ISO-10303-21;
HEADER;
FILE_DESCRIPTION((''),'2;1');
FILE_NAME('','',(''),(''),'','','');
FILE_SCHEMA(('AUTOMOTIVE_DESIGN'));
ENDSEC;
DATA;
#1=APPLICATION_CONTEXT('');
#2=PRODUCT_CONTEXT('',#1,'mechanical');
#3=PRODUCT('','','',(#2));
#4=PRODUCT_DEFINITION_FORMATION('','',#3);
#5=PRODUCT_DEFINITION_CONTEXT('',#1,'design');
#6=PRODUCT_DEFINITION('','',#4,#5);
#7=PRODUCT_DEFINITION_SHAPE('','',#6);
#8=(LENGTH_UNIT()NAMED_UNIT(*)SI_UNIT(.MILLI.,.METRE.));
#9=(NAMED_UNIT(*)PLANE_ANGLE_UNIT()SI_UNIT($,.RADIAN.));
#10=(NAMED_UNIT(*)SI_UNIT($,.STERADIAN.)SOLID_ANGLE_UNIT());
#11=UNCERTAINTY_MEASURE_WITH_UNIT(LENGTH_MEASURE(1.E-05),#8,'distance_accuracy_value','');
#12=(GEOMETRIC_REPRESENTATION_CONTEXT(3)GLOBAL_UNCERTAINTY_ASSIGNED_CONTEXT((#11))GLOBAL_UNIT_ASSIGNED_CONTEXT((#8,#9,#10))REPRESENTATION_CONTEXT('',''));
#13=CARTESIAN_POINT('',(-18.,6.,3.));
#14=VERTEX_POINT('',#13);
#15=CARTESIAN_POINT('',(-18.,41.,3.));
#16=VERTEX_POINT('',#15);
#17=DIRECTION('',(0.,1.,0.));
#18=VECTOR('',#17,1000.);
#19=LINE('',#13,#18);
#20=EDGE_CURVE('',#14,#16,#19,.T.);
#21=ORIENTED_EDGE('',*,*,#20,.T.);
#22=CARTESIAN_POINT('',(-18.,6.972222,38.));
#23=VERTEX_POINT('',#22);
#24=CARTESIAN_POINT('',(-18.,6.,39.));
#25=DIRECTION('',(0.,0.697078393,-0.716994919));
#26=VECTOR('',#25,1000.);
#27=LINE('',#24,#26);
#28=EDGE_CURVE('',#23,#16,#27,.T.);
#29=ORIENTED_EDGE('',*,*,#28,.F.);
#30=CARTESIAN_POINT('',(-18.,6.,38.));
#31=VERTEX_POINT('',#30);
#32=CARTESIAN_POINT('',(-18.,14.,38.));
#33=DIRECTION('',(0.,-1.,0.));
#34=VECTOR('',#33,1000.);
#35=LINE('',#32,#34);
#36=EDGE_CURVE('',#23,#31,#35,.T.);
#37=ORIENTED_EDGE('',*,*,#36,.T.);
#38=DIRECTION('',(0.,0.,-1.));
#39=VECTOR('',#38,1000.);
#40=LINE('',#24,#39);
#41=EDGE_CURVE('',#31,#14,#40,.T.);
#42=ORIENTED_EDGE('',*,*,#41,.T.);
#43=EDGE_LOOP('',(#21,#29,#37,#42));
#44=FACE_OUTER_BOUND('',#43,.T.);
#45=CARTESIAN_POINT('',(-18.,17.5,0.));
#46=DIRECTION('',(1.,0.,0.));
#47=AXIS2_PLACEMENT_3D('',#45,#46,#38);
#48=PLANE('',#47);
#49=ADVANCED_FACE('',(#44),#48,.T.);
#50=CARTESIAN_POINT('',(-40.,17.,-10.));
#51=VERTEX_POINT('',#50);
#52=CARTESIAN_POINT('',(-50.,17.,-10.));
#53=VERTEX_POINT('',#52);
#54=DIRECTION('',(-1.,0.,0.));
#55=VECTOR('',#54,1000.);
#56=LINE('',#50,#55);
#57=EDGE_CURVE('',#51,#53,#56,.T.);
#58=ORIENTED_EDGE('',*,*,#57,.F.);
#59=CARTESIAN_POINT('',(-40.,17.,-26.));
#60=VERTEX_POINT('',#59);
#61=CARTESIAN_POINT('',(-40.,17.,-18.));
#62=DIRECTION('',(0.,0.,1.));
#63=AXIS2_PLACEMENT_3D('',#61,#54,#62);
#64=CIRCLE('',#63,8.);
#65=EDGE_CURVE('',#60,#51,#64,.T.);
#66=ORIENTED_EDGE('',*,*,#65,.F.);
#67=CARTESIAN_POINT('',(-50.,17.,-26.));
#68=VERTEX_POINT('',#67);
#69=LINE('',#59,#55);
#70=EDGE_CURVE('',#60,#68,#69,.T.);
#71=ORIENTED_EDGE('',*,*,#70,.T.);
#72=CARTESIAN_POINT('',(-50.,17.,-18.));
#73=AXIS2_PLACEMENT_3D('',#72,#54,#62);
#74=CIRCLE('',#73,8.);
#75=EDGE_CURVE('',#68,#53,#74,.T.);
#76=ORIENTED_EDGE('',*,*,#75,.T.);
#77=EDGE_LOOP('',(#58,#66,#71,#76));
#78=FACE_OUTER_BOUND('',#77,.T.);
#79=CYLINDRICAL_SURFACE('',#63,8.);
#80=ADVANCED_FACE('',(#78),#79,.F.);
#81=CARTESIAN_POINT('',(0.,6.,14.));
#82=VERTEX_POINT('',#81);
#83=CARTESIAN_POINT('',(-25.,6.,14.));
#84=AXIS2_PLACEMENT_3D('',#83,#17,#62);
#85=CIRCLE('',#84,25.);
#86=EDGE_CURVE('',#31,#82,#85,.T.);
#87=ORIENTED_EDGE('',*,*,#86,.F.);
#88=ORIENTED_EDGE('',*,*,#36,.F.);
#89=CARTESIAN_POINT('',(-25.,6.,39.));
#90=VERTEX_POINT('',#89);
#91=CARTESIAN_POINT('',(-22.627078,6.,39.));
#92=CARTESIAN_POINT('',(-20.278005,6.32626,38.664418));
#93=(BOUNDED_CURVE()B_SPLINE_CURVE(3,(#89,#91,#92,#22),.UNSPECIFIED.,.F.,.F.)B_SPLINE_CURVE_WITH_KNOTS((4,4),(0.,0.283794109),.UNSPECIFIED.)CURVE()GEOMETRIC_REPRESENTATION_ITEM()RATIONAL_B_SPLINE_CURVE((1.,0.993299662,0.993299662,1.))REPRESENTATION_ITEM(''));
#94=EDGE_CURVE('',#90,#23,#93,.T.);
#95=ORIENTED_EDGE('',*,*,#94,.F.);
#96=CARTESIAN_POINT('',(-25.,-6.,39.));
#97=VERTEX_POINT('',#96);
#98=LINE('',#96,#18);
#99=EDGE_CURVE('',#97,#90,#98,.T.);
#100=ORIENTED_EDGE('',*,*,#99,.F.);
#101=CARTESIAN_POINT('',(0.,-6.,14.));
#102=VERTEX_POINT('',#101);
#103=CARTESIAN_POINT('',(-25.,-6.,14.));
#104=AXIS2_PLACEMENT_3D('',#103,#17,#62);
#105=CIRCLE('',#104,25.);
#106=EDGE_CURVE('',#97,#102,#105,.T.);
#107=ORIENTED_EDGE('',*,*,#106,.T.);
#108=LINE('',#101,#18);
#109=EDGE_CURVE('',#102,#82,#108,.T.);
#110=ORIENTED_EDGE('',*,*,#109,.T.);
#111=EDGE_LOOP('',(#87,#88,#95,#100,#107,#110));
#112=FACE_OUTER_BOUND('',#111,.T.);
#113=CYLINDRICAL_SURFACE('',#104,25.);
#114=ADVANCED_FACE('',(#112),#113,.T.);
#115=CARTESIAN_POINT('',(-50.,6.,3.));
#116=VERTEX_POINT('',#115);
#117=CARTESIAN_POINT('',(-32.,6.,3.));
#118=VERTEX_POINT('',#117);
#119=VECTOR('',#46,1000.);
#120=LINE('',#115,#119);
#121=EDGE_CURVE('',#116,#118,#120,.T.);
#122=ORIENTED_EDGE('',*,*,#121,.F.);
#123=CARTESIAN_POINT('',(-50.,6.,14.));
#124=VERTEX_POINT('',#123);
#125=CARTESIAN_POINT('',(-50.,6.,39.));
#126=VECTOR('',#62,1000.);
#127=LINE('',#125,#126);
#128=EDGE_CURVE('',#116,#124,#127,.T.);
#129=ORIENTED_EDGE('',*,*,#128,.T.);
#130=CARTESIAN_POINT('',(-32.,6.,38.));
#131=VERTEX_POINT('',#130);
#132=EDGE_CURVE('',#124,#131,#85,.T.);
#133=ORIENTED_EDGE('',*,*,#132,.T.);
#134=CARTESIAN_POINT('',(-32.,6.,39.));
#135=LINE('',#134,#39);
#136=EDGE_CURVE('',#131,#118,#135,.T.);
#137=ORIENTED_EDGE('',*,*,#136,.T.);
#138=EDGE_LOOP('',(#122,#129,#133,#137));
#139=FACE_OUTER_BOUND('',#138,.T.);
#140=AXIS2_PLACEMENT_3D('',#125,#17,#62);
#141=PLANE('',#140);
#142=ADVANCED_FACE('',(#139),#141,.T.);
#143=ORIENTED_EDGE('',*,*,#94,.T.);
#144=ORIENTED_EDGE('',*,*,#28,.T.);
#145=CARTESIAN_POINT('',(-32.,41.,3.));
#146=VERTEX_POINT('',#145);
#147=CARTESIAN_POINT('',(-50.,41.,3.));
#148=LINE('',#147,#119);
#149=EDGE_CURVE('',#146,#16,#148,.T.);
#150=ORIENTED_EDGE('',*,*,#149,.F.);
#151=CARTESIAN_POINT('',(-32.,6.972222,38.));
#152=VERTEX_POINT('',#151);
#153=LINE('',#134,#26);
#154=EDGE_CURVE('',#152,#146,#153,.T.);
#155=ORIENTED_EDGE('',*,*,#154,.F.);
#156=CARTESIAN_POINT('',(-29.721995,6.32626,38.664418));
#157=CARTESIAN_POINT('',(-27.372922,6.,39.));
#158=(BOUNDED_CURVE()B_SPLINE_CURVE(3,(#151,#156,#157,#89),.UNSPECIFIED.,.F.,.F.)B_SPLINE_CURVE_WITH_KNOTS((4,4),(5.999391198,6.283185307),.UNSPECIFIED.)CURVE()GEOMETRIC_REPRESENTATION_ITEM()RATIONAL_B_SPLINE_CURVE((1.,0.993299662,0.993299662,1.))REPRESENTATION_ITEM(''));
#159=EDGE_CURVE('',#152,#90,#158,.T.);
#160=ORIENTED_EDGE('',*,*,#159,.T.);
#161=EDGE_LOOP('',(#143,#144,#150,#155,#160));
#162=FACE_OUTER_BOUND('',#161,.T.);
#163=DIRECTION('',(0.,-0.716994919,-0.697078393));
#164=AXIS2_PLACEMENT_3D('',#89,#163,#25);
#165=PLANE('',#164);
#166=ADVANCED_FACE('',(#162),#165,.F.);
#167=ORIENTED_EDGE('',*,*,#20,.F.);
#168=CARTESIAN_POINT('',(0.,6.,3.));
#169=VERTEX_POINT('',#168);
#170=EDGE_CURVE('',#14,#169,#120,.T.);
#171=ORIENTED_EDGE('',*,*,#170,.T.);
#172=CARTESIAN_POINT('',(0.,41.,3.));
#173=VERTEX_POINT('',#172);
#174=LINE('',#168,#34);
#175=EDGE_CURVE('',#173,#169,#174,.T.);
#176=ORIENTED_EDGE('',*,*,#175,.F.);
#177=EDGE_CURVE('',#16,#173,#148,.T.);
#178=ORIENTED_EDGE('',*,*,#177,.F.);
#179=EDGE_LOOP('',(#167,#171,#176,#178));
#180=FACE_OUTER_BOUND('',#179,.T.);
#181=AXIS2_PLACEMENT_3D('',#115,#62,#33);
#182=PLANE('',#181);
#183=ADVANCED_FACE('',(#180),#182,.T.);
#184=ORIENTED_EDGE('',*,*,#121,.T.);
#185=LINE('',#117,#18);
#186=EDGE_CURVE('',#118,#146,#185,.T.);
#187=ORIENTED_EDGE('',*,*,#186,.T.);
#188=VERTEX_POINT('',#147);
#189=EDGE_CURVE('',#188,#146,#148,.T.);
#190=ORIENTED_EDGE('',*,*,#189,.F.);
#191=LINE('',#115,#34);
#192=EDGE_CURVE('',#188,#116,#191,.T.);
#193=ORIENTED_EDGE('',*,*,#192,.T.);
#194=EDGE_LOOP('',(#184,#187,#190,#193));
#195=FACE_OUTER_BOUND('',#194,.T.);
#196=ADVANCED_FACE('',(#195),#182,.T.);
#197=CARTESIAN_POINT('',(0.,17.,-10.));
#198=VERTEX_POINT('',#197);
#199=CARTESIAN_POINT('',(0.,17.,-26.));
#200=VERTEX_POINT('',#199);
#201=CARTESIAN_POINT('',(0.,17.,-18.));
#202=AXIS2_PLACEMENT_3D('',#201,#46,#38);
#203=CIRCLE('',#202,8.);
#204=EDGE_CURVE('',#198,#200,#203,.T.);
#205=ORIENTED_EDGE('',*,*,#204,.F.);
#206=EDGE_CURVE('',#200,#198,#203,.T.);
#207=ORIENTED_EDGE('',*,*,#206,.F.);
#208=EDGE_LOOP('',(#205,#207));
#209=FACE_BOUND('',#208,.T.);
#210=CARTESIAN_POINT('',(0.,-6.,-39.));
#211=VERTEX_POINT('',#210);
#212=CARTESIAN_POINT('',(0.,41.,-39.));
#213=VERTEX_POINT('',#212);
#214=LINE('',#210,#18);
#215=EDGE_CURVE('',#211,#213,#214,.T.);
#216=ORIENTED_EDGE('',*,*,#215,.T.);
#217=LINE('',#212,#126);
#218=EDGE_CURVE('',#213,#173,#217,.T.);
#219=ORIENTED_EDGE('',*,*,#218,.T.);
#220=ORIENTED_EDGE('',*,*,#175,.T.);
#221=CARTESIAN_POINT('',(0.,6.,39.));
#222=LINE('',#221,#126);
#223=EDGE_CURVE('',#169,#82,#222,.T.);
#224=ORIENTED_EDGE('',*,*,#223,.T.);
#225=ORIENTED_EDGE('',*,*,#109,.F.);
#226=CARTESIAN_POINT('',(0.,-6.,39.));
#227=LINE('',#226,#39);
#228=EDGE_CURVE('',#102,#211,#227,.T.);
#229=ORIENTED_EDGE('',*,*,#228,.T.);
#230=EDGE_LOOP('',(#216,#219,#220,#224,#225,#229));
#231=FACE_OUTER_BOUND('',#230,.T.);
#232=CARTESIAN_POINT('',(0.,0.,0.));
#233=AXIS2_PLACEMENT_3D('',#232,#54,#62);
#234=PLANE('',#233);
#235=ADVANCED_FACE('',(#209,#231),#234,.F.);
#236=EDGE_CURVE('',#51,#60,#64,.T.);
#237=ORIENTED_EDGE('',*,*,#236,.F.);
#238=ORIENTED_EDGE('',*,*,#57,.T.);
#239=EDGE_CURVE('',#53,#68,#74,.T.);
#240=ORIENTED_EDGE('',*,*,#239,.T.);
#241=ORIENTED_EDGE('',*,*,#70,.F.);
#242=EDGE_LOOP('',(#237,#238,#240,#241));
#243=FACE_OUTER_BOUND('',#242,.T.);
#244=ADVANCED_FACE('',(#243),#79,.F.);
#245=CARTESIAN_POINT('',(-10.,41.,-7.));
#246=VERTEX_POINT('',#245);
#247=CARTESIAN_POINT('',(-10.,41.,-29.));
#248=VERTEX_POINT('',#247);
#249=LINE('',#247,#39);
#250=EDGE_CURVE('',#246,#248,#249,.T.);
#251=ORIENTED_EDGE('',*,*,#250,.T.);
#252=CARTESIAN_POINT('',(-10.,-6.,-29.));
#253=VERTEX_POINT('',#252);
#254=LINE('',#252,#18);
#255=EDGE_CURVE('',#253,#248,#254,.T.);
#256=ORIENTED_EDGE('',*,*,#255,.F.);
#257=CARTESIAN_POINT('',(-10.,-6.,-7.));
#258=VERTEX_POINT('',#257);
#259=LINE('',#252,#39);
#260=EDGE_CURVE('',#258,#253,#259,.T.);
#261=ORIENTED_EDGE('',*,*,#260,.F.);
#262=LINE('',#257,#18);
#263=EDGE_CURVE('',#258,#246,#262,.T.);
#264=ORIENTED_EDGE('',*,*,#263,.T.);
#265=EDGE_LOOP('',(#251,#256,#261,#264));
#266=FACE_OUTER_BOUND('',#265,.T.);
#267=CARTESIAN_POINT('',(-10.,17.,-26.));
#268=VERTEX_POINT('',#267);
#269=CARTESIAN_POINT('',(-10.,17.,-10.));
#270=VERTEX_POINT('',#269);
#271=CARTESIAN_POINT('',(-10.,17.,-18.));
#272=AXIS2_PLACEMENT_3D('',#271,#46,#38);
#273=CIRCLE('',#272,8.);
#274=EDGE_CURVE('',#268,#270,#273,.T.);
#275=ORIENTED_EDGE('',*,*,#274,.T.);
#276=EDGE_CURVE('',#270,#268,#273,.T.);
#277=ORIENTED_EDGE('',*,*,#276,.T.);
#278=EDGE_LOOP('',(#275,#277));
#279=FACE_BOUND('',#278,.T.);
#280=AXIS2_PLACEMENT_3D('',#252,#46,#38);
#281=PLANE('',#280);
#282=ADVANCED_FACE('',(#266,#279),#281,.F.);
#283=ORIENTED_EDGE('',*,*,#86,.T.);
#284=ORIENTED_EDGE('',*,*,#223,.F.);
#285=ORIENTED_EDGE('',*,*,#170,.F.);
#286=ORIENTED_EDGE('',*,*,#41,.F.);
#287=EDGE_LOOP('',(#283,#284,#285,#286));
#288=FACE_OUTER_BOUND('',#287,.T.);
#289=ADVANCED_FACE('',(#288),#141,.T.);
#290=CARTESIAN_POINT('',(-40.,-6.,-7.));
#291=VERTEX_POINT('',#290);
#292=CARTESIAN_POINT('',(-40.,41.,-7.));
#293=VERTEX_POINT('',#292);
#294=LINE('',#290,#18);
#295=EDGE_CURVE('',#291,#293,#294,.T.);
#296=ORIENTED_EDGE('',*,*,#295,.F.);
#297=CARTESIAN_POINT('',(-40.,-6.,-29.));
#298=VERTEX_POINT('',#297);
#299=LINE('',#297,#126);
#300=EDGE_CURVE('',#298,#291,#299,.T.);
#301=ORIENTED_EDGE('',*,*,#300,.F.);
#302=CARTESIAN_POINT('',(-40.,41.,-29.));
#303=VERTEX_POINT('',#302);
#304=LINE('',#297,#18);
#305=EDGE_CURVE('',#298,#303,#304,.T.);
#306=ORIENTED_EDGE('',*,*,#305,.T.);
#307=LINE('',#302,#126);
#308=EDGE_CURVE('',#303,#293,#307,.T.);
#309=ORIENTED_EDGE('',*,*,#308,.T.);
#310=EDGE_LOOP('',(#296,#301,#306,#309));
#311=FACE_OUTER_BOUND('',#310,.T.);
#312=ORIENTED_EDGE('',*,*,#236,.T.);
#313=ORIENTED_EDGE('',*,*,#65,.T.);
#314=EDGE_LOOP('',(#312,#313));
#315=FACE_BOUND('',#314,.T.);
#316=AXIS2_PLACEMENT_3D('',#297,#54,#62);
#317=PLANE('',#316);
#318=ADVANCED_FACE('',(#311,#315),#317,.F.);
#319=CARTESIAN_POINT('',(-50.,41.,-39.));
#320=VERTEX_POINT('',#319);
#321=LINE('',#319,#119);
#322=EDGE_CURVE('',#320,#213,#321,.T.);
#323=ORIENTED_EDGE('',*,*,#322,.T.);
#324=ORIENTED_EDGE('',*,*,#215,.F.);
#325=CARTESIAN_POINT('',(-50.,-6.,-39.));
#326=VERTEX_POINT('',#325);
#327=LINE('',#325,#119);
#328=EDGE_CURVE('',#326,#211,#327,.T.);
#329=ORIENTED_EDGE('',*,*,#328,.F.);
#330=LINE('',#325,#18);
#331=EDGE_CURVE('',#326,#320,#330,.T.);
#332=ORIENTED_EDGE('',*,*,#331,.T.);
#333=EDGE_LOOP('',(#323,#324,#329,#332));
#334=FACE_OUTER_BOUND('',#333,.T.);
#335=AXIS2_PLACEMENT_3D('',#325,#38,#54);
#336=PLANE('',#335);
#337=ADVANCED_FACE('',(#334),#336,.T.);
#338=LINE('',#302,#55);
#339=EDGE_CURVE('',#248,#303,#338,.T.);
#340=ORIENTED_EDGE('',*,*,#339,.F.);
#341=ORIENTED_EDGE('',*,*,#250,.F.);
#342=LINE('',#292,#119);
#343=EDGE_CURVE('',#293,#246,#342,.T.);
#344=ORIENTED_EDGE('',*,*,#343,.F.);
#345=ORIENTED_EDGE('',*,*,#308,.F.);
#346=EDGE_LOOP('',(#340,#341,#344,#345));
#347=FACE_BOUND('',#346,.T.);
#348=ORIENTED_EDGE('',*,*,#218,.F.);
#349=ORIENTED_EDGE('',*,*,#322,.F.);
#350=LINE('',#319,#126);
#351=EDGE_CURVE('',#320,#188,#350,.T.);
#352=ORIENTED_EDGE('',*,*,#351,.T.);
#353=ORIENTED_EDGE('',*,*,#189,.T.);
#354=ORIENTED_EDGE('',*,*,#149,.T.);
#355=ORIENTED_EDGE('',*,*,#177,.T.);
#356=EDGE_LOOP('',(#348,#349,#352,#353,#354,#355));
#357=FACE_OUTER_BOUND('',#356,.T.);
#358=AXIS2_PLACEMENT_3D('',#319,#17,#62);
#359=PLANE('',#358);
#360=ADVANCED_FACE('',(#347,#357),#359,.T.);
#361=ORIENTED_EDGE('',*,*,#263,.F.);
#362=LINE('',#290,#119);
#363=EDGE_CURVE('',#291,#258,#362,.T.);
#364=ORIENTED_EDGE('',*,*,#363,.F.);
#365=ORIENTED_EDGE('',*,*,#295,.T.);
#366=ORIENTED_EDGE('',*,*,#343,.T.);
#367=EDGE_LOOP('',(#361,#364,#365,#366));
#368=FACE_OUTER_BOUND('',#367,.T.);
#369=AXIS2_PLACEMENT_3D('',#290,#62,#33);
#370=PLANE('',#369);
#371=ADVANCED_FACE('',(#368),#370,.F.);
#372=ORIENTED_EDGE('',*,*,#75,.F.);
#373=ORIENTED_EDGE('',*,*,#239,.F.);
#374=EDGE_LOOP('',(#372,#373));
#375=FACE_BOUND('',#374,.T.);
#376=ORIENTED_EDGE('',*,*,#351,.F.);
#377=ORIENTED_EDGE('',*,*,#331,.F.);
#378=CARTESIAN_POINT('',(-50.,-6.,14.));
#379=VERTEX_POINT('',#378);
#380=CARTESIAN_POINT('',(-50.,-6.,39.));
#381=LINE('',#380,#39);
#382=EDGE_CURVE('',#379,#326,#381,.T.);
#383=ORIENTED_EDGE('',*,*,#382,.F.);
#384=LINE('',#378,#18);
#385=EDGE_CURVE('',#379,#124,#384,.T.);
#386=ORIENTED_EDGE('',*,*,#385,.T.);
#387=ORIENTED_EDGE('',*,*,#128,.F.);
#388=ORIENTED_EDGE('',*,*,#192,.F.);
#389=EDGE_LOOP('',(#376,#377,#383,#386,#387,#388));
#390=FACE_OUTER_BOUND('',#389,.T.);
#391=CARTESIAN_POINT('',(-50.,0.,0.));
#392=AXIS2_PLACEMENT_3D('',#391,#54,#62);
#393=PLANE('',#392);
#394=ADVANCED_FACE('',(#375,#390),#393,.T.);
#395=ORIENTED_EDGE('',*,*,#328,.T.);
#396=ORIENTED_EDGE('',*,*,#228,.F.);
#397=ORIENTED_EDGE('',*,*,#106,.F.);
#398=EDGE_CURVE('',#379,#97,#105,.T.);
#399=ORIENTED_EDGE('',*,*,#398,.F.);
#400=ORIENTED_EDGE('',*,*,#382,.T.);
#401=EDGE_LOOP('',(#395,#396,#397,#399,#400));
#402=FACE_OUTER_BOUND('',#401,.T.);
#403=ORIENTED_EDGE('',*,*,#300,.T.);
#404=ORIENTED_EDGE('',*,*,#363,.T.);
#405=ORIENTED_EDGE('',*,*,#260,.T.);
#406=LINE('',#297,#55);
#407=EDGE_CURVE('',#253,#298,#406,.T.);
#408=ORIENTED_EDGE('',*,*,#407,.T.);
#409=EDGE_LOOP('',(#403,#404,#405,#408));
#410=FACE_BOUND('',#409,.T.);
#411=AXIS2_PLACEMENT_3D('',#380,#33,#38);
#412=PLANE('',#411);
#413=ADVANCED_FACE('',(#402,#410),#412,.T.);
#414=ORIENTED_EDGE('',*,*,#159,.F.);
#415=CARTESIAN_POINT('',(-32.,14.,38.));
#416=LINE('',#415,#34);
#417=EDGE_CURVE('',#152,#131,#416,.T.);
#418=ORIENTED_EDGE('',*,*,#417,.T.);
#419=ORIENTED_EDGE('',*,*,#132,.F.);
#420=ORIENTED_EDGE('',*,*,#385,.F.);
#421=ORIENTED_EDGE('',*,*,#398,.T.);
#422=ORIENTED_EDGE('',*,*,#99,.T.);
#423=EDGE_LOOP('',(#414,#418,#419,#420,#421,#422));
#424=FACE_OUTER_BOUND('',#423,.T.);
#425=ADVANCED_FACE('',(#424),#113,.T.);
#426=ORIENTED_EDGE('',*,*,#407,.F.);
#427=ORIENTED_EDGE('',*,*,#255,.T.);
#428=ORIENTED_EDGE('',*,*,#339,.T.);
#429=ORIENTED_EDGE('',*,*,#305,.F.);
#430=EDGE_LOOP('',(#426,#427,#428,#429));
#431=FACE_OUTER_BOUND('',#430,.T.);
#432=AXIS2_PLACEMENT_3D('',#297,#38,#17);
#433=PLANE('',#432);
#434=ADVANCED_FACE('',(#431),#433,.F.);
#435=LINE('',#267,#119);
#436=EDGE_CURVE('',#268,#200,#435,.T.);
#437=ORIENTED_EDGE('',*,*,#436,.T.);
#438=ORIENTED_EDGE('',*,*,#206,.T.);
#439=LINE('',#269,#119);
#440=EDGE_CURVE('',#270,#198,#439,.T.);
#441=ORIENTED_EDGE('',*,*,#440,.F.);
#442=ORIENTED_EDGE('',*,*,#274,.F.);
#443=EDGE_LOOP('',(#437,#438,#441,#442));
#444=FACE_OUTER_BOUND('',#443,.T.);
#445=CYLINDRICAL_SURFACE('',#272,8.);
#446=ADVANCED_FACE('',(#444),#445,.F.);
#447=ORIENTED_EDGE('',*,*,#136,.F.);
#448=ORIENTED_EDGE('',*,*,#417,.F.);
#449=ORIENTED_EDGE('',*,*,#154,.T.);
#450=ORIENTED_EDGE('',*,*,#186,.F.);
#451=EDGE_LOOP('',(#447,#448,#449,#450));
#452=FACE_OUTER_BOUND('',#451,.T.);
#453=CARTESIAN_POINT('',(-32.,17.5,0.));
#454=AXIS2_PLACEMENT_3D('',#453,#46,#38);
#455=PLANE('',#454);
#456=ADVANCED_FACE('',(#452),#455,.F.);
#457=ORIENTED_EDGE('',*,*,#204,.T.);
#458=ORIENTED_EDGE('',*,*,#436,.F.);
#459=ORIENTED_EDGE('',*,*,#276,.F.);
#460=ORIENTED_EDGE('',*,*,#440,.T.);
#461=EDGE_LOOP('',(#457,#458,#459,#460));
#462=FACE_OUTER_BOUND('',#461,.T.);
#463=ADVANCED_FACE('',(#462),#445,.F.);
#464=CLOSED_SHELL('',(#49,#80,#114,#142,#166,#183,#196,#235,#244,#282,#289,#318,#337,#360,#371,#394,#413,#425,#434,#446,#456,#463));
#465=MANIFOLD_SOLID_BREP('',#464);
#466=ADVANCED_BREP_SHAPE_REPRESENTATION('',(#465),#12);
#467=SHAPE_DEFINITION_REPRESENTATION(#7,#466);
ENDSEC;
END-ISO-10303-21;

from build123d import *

# Parameters (mm, degrees)
BASE_PLATE_SKETCH_W      = 78
BASE_PLATE_SKETCH_H      = 12
BASE_PLATE_DEPTH         = 50
UPRIGHT_BLOCK_SKETCH_W   = 42
UPRIGHT_BLOCK_SKETCH_H   = 35
UPRIGHT_BLOCK_DEPTH      = 50
BLOCK_POCKET_SKETCH_W    = 30
BLOCK_POCKET_SKETCH_H    = 22
BLOCK_POCKET_30X22_DEPTH = 79.930349043
SIDE_CUT_1_SKETCH_R      = 8
SIDE_CUT_1_DEPTH         = 10
SIDE_START               = -10
SIDE_CUT_2_SKETCH_R      = 8
SIDE_CUT_2_DEPTH         = 10
GUSSET_RIB_14MM_REACH    = 63.863
GUSSET_RIB_SKETCH_WALL_W = 175.935063468
GUSSET_RIB_SKETCH_WALL_H = 14
FRONT_PROFILE_CUT_DEPTH  = 73.429275849
RIB_START                = -20
RIB_TRIM_CUT_DEPTH       = 20


with BuildPart() as part:
    # Base Plate Sketch → Base Plate (new body)
    with BuildSketch(Plane(origin=(0, 0, 0), x_dir=(0, 0, -1), z_dir=(1, 0, 0))):
        Rectangle(BASE_PLATE_SKETCH_W, BASE_PLATE_SKETCH_H)
    extrude(amount=-BASE_PLATE_DEPTH)

    # Upright Block Sketch → Upright Block (add)
    with BuildSketch(Plane(origin=(0, 0, 0), x_dir=(0, 0, -1), z_dir=(1, 0, 0))):
        with Locations((18, 23.5)):
            Rectangle(UPRIGHT_BLOCK_SKETCH_W, UPRIGHT_BLOCK_SKETCH_H)
    extrude(amount=-UPRIGHT_BLOCK_DEPTH)

    # Block Pocket Sketch → Block Pocket 30x22 (cut, through all)
    with BuildSketch(Plane(origin=(0, 41, 0), x_dir=(1, 0, 0), z_dir=(0, 1, 0))):
        with Locations((-25, 18)):
            Rectangle(BLOCK_POCKET_SKETCH_W, BLOCK_POCKET_SKETCH_H)
    extrude(amount=-BLOCK_POCKET_30X22_DEPTH, mode=Mode.SUBTRACT)

    # Side Cut 1 Sketch → Side Cut 1 (cut)
    with BuildSketch(Plane(origin=(0, 0, 0), x_dir=(0, 0, -1), z_dir=(1, 0, 0))):
        with Locations((18, 17)):
            Circle(SIDE_CUT_1_SKETCH_R)
    extrude(amount=-SIDE_CUT_1_DEPTH, mode=Mode.SUBTRACT)

    # Side Cut 2 Sketch → Side Cut 2 (cut)
    with BuildSketch(Plane.ZY.offset(50).offset(SIDE_START)):
        with Locations(Location((-18, 17, 0), (0, 0, 180))):
            Circle(SIDE_CUT_2_SKETCH_R)
    extrude(amount=SIDE_CUT_2_DEPTH, mode=Mode.SUBTRACT)

    # Gusset Rib Sketch wall → Gusset Rib 14mm (add, up to next)
    with BuildSketch(Plane(origin=(-25, 23.5, 21), x_dir=(0, 0.697078393292, -0.716994918814), z_dir=(0, 0.716994918814, 0.697078393292)), mode=Mode.PRIVATE) as gusset_rib_14mm_sk1:
        Rectangle(GUSSET_RIB_SKETCH_WALL_W, GUSSET_RIB_SKETCH_WALL_H)
    gusset_rib_14mm_tool1 = extrude(gusset_rib_14mm_sk1.sketch, amount=-GUSSET_RIB_14MM_REACH, mode=Mode.PRIVATE) - part.part
    add(gusset_rib_14mm_tool1.solids().sort_by_distance((-25, 23.5, 21))[0])

    # Front Profile Cut Sketch → Front Profile Cut (cut, through all)
    with BuildSketch(Plane(origin=(0, 6, 0), x_dir=(1, 0, 0), z_dir=(0, 1, 0))):
        with BuildLine():
            Line((-50, -39), (-25, -39))
            ThreePointArc((-25, -39), (-42.67766953, -31.67766953), (-50, -14))
            Line((-50, -14), (-50, -39))
        make_face()
        with BuildLine():
            Line((-18, -38), (-18, -39))
            Line((-18, -39), (0, -39))
            Line((0, -39), (0, -14))
            ThreePointArc((0, -14), (-5, -29), (-18, -38))
        make_face()
    extrude(amount=-FRONT_PROFILE_CUT_DEPTH, mode=Mode.SUBTRACT)

    # Rib Trim Cut Sketch → Rib Trim Cut (cut)
    with BuildSketch(Plane.XZ.offset(6).offset(RIB_START)):
        with BuildLine():
            Line((-25, 39), (-32, 39))
            Line((-32, 39), (-32, 38))
            ThreePointArc((-32, 38), (-28.535533906, 38.748737342), (-25, 39))
        make_face()
        with BuildLine():
            ThreePointArc((-18, 38), (-21.464466094, 38.748737342), (-25, 39))
            Line((-25, 39), (-18, 39))
            Line((-18, 39), (-18, 38))
        make_face()
    extrude(amount=RIB_TRIM_CUT_DEPTH, mode=Mode.SUBTRACT)


solid = part.part
